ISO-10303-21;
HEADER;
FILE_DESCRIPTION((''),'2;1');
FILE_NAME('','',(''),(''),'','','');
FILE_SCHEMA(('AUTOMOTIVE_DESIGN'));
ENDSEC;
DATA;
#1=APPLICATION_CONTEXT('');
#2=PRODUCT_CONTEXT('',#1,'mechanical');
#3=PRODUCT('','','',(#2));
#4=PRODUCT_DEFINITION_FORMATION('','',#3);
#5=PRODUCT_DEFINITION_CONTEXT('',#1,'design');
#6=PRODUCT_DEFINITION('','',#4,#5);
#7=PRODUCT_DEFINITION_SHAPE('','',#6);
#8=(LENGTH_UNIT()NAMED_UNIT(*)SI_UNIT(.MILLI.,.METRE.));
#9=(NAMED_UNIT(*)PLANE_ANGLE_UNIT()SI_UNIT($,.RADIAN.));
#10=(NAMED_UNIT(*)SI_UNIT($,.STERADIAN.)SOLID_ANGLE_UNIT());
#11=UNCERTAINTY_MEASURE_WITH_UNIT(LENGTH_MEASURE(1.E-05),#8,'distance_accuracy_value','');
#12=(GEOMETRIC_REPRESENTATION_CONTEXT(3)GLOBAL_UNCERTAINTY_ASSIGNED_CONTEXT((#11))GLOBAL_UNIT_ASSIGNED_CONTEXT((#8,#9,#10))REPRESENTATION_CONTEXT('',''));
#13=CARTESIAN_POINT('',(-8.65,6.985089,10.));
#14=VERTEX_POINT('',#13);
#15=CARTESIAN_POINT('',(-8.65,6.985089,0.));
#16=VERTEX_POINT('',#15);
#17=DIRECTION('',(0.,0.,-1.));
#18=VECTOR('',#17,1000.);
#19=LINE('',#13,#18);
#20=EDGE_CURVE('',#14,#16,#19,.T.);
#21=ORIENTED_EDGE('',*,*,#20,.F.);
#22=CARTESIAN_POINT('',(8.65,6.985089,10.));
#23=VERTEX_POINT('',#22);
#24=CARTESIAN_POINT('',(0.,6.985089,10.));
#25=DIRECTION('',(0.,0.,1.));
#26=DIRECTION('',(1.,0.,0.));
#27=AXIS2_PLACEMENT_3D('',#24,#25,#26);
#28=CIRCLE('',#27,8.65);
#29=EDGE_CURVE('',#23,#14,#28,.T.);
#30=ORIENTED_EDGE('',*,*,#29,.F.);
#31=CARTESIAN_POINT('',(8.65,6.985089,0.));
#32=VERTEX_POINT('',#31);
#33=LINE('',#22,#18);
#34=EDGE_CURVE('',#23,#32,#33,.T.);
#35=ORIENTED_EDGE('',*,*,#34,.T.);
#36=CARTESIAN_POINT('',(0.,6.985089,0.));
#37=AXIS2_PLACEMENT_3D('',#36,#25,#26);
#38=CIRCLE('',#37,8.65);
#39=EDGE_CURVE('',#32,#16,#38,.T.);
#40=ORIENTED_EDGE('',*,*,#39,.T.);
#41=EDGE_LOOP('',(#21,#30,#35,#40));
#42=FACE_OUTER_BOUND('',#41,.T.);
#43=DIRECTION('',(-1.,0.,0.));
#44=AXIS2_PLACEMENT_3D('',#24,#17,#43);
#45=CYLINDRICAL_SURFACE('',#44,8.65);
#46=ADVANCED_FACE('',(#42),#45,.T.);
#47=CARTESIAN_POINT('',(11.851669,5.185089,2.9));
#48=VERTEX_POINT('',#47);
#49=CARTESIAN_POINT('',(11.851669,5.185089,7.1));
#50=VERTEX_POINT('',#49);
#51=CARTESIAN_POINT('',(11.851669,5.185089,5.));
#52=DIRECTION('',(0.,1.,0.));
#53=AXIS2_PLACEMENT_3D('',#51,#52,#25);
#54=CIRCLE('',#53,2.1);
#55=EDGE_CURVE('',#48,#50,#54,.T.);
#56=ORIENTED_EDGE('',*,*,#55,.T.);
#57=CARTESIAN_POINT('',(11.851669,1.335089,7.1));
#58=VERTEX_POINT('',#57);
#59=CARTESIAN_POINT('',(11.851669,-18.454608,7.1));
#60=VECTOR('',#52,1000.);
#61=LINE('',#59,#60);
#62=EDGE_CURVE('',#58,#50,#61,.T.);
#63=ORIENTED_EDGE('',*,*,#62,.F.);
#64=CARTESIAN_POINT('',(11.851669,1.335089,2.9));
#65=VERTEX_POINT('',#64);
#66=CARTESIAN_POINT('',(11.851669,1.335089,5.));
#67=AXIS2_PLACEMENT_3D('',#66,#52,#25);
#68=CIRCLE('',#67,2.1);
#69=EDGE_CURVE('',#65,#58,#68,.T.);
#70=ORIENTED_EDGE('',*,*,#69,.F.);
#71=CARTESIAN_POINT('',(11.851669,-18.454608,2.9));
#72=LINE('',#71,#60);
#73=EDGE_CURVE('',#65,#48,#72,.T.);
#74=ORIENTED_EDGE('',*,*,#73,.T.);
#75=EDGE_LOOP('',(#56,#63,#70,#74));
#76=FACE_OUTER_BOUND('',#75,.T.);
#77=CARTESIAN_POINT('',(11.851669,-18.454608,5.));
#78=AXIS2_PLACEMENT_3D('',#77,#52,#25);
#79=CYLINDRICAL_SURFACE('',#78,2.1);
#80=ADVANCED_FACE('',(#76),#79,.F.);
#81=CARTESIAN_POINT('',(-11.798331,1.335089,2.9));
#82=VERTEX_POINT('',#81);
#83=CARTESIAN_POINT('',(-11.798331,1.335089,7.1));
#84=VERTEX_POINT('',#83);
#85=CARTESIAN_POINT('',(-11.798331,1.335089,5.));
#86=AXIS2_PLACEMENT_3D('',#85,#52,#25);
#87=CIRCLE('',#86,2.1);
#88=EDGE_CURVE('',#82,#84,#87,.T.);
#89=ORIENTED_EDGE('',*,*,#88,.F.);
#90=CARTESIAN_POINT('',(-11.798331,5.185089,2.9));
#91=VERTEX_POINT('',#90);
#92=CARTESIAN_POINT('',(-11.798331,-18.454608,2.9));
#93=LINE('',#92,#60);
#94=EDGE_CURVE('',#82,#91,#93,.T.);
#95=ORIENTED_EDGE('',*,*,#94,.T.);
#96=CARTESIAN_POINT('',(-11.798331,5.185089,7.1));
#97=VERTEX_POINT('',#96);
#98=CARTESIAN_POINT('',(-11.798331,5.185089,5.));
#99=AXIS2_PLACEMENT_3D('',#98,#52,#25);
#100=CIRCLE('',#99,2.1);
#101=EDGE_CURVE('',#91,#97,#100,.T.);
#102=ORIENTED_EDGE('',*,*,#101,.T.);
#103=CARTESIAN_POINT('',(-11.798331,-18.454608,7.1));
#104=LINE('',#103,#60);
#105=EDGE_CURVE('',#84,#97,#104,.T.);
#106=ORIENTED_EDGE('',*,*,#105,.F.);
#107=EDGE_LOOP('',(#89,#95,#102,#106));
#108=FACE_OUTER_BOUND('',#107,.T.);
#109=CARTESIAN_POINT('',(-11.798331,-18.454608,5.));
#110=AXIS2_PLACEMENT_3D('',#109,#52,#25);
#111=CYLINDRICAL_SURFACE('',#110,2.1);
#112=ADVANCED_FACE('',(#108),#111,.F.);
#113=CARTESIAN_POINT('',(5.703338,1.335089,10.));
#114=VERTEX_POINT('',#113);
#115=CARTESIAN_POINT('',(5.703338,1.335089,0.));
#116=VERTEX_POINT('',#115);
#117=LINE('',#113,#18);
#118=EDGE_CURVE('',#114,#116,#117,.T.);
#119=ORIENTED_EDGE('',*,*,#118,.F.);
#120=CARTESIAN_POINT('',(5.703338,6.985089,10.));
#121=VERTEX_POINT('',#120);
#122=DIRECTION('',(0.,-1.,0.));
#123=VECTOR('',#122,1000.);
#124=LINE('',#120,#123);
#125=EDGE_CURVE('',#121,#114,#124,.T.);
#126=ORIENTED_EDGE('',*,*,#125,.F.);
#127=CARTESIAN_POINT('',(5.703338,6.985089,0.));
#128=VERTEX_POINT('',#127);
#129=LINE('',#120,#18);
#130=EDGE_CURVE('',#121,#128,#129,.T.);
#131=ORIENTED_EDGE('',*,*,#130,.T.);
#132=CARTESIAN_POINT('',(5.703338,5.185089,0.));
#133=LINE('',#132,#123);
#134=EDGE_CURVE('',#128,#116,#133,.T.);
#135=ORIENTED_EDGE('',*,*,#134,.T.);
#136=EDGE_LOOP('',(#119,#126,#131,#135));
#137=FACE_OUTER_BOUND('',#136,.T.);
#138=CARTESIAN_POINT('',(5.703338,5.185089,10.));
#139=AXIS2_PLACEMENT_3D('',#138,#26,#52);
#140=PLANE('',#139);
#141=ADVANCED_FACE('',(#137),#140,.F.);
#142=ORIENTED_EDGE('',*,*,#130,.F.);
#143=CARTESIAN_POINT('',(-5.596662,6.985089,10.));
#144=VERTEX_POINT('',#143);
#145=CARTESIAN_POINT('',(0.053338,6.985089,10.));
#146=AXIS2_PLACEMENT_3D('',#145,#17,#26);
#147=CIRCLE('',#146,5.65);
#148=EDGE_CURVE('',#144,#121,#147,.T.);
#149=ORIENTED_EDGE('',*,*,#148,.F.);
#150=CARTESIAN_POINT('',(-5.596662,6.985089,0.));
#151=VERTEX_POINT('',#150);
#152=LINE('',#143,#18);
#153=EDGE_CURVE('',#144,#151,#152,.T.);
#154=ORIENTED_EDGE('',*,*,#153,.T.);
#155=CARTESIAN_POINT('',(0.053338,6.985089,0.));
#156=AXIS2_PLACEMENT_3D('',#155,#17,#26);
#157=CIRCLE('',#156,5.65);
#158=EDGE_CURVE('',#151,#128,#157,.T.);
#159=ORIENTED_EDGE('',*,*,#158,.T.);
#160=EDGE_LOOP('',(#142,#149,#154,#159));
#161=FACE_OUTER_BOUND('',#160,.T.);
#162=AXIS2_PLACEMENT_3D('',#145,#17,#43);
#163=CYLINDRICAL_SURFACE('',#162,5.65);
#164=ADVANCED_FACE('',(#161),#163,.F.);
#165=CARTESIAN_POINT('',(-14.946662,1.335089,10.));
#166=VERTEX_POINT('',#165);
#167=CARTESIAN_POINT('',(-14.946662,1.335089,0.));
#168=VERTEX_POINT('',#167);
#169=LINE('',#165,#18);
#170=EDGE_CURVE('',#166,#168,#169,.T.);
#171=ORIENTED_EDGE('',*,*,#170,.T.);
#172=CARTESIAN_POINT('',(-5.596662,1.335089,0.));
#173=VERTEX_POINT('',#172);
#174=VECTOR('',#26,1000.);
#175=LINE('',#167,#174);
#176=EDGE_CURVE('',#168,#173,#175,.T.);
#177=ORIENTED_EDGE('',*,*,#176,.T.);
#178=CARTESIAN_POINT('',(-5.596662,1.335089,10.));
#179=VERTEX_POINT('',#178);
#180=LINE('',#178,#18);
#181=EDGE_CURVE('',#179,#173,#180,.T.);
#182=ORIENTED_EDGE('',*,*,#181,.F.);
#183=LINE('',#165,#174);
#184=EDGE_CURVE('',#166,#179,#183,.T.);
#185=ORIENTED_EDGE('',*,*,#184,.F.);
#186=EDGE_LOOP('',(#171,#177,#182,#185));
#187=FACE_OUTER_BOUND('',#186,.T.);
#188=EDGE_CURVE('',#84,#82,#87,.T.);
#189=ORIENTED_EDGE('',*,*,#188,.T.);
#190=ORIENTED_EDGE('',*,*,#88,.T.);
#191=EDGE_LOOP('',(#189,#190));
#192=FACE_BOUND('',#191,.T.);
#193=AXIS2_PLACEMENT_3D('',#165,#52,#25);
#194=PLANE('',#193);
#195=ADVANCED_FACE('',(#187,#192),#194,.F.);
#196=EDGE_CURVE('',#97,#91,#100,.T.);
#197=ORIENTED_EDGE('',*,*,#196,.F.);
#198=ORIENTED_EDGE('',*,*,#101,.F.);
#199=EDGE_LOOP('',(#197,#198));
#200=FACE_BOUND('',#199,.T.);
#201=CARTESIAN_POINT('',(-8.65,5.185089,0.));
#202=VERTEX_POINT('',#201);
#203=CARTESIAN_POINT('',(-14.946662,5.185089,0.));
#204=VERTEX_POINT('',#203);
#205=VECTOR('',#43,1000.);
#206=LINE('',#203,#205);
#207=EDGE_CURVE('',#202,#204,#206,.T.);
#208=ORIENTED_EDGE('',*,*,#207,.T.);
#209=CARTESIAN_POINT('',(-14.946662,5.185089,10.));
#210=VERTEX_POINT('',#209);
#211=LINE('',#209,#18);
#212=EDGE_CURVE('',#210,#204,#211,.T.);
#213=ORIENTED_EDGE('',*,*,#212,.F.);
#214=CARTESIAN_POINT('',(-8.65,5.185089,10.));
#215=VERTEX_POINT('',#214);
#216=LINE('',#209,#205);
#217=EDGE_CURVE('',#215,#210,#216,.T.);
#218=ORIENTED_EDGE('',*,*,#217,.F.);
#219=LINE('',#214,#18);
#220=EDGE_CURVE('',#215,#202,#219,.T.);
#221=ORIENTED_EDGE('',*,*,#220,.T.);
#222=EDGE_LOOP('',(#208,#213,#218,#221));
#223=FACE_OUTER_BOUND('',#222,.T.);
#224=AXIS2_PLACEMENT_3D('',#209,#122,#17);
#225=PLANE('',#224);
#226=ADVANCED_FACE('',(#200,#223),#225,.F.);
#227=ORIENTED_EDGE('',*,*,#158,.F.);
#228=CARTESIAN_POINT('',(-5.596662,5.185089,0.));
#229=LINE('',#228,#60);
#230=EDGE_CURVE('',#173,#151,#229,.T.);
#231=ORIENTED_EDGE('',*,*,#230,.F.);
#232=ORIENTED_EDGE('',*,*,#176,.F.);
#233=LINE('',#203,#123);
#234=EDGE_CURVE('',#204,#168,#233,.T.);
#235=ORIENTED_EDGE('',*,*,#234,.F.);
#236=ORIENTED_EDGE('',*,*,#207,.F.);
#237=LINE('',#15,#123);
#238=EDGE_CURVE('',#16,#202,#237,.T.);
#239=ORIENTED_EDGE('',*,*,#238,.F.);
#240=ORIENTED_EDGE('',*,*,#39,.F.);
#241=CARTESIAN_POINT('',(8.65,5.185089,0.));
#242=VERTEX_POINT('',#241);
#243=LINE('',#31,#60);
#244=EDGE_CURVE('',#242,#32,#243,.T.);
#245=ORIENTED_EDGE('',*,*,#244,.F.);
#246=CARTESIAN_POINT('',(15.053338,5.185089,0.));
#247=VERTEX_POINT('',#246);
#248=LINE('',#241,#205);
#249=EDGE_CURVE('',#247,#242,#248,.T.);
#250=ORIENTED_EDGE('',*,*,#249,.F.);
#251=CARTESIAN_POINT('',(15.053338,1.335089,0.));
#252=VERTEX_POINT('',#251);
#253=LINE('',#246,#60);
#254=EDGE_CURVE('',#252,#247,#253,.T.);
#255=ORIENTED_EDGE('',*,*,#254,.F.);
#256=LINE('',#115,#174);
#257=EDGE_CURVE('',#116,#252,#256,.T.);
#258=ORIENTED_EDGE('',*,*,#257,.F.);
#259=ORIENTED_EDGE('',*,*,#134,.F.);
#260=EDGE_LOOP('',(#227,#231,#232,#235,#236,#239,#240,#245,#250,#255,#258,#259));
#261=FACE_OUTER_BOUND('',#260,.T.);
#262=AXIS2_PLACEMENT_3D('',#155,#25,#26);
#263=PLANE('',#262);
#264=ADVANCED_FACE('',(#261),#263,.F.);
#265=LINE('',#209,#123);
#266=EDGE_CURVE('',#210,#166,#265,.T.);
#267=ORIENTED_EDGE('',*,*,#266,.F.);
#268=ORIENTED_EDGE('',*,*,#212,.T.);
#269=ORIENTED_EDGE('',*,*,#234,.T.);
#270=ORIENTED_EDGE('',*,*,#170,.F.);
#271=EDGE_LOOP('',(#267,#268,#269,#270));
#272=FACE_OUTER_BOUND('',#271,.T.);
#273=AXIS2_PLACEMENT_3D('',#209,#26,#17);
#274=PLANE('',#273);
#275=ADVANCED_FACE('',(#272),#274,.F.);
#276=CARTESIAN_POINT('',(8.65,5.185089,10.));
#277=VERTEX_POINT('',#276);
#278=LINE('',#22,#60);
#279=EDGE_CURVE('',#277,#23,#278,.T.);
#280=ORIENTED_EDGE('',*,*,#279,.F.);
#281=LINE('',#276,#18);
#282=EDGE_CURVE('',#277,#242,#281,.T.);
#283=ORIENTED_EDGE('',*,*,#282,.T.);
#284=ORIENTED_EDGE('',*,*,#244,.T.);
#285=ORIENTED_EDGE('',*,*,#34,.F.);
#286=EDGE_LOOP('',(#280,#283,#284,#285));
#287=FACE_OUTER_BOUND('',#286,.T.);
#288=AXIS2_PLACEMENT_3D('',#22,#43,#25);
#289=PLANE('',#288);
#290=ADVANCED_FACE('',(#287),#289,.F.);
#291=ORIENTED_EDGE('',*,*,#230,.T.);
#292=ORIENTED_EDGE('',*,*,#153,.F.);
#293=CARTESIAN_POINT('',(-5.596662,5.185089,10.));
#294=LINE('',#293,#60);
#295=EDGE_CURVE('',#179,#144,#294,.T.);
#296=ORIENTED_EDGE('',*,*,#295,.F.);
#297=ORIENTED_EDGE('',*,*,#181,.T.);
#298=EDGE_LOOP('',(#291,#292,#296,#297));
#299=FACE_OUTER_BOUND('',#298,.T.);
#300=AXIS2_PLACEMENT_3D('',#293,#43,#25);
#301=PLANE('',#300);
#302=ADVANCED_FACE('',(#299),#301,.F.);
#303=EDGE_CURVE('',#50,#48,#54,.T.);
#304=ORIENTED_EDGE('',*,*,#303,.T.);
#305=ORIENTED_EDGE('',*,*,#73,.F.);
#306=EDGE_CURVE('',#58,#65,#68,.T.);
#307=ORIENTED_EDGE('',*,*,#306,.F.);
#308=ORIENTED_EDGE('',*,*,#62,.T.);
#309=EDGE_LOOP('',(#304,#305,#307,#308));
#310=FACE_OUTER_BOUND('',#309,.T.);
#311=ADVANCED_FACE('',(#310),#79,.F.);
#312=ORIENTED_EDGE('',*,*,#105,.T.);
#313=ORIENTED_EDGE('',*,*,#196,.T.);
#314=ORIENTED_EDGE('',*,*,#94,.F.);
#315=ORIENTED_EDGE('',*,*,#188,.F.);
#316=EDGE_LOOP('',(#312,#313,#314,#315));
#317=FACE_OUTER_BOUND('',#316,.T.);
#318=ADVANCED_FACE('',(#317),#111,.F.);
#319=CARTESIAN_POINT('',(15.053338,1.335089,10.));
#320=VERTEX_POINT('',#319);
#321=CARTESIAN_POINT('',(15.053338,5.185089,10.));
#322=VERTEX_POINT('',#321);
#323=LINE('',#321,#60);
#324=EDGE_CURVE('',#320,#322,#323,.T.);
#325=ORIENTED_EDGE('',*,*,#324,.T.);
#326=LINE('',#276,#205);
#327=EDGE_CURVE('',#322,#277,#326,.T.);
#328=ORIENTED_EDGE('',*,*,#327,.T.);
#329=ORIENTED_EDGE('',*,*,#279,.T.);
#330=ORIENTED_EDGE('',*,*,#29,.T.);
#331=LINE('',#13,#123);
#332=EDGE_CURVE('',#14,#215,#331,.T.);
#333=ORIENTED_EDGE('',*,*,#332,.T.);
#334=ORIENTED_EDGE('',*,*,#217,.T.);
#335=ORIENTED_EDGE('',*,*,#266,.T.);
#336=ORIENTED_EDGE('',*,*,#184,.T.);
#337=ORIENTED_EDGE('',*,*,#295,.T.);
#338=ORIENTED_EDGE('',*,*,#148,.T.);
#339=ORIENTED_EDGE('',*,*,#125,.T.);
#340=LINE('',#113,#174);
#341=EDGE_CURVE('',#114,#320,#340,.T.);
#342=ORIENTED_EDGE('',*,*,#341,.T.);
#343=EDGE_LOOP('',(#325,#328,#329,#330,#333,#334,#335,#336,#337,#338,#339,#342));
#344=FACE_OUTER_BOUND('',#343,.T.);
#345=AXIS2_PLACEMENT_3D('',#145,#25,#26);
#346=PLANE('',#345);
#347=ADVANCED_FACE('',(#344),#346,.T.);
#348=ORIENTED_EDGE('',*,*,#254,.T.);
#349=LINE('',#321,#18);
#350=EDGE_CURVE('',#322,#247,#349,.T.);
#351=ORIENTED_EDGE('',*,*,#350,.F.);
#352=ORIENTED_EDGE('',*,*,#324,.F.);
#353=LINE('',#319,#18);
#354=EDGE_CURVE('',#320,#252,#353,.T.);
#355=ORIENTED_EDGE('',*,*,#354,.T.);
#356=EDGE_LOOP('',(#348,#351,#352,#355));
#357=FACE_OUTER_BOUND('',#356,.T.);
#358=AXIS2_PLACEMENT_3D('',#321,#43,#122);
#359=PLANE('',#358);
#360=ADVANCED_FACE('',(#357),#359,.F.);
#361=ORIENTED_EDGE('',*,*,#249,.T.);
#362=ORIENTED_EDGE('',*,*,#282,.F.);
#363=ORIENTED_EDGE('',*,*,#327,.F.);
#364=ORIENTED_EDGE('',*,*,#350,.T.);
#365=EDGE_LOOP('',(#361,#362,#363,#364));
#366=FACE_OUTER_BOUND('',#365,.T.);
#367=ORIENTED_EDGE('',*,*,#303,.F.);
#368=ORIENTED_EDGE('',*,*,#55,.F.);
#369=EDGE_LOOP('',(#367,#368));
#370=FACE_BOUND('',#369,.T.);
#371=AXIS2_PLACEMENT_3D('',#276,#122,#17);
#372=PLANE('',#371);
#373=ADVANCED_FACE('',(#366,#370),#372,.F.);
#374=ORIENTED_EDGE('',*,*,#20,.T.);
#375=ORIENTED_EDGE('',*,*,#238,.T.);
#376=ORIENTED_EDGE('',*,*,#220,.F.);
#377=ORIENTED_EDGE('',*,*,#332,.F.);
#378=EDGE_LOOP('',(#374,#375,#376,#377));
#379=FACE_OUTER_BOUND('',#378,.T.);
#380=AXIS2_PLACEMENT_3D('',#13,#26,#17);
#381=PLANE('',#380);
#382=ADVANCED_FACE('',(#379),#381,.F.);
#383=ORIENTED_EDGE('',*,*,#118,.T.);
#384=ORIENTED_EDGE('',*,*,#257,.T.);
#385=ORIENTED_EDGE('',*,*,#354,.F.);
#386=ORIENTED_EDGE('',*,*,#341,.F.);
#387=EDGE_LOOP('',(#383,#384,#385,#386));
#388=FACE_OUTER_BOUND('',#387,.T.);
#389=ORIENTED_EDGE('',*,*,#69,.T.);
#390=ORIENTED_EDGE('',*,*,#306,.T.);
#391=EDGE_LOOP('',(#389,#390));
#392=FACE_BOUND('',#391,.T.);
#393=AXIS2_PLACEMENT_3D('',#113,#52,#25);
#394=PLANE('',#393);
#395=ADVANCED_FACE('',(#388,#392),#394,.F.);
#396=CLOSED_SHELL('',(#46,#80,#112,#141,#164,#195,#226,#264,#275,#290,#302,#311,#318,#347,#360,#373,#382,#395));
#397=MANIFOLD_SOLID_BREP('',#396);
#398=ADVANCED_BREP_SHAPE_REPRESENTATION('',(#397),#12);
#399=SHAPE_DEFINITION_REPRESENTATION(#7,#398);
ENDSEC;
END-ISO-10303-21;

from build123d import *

# Parameters (mm, degrees)
EXTRUDE_1_DEPTH     = 10
SKETCH_2_R          = 2.1
CUT_EXTRUDE_1_DEPTH = 17.7


with BuildPart() as part:
    # 草图1 → 凸台-拉伸1 (new body)
    with BuildSketch(Plane.XY):
        with BuildLine():
            Line((-5.596661991, 5.185089456), (-5.596661991, 6.985089456))
            ThreePointArc((-5.596661991, 6.985089456), (0.053338009, 12.635089456), (5.703338009, 6.985089456))
            Line((5.703338009, 6.985089456), (5.703338009, 5.185089456))
            Line((5.703338009, 5.185089456), (5.703338009, 1.335089456))
            Line((5.703338009, 1.335089456), (15.053338009, 1.335089456))
            Line((15.053338009, 1.335089456), (15.053338009, 5.185089456))
            Line((15.053338009, 5.185089456), (8.65, 5.185089456))
            Line((8.65, 5.185089456), (8.65, 6.985089456))
            ThreePointArc((8.65, 6.985089456), (0, 15.635089456), (-8.65, 6.985089456))
            Line((-8.65, 6.985089456), (-8.65, 5.185089456))
            Line((-8.65, 5.185089456), (-14.946661991, 5.185089456))
            Line((-14.946661991, 5.185089456), (-14.946661991, 1.335089456))
            Line((-14.946661991, 1.335089456), (-5.596661991, 1.335089456))
            Line((-5.596661991, 1.335089456), (-5.596661991, 5.185089456))
        make_face()
    extrude(amount=EXTRUDE_1_DEPTH)

    # 草图2 → 切除-拉伸1 (cut)
    with BuildSketch(Plane(origin=(-970.090594905, 5.185089456, 1019.250263045), x_dir=(0, 0, 1), z_dir=(0, 1, 0))):
        with Locations((-1055.250263055, 981.942263912)):
            Circle(SKETCH_2_R)
        with Locations((-1055.250263055, 958.292263912)):
            Circle(SKETCH_2_R)
        with Locations((-1014.250263055, 958.292263912)):
            Circle(SKETCH_2_R)
        with Locations((-1014.250263055, 981.942263912)):
            Circle(SKETCH_2_R)
    extrude(amount=-CUT_EXTRUDE_1_DEPTH, mode=Mode.SUBTRACT)


solid = part.part
